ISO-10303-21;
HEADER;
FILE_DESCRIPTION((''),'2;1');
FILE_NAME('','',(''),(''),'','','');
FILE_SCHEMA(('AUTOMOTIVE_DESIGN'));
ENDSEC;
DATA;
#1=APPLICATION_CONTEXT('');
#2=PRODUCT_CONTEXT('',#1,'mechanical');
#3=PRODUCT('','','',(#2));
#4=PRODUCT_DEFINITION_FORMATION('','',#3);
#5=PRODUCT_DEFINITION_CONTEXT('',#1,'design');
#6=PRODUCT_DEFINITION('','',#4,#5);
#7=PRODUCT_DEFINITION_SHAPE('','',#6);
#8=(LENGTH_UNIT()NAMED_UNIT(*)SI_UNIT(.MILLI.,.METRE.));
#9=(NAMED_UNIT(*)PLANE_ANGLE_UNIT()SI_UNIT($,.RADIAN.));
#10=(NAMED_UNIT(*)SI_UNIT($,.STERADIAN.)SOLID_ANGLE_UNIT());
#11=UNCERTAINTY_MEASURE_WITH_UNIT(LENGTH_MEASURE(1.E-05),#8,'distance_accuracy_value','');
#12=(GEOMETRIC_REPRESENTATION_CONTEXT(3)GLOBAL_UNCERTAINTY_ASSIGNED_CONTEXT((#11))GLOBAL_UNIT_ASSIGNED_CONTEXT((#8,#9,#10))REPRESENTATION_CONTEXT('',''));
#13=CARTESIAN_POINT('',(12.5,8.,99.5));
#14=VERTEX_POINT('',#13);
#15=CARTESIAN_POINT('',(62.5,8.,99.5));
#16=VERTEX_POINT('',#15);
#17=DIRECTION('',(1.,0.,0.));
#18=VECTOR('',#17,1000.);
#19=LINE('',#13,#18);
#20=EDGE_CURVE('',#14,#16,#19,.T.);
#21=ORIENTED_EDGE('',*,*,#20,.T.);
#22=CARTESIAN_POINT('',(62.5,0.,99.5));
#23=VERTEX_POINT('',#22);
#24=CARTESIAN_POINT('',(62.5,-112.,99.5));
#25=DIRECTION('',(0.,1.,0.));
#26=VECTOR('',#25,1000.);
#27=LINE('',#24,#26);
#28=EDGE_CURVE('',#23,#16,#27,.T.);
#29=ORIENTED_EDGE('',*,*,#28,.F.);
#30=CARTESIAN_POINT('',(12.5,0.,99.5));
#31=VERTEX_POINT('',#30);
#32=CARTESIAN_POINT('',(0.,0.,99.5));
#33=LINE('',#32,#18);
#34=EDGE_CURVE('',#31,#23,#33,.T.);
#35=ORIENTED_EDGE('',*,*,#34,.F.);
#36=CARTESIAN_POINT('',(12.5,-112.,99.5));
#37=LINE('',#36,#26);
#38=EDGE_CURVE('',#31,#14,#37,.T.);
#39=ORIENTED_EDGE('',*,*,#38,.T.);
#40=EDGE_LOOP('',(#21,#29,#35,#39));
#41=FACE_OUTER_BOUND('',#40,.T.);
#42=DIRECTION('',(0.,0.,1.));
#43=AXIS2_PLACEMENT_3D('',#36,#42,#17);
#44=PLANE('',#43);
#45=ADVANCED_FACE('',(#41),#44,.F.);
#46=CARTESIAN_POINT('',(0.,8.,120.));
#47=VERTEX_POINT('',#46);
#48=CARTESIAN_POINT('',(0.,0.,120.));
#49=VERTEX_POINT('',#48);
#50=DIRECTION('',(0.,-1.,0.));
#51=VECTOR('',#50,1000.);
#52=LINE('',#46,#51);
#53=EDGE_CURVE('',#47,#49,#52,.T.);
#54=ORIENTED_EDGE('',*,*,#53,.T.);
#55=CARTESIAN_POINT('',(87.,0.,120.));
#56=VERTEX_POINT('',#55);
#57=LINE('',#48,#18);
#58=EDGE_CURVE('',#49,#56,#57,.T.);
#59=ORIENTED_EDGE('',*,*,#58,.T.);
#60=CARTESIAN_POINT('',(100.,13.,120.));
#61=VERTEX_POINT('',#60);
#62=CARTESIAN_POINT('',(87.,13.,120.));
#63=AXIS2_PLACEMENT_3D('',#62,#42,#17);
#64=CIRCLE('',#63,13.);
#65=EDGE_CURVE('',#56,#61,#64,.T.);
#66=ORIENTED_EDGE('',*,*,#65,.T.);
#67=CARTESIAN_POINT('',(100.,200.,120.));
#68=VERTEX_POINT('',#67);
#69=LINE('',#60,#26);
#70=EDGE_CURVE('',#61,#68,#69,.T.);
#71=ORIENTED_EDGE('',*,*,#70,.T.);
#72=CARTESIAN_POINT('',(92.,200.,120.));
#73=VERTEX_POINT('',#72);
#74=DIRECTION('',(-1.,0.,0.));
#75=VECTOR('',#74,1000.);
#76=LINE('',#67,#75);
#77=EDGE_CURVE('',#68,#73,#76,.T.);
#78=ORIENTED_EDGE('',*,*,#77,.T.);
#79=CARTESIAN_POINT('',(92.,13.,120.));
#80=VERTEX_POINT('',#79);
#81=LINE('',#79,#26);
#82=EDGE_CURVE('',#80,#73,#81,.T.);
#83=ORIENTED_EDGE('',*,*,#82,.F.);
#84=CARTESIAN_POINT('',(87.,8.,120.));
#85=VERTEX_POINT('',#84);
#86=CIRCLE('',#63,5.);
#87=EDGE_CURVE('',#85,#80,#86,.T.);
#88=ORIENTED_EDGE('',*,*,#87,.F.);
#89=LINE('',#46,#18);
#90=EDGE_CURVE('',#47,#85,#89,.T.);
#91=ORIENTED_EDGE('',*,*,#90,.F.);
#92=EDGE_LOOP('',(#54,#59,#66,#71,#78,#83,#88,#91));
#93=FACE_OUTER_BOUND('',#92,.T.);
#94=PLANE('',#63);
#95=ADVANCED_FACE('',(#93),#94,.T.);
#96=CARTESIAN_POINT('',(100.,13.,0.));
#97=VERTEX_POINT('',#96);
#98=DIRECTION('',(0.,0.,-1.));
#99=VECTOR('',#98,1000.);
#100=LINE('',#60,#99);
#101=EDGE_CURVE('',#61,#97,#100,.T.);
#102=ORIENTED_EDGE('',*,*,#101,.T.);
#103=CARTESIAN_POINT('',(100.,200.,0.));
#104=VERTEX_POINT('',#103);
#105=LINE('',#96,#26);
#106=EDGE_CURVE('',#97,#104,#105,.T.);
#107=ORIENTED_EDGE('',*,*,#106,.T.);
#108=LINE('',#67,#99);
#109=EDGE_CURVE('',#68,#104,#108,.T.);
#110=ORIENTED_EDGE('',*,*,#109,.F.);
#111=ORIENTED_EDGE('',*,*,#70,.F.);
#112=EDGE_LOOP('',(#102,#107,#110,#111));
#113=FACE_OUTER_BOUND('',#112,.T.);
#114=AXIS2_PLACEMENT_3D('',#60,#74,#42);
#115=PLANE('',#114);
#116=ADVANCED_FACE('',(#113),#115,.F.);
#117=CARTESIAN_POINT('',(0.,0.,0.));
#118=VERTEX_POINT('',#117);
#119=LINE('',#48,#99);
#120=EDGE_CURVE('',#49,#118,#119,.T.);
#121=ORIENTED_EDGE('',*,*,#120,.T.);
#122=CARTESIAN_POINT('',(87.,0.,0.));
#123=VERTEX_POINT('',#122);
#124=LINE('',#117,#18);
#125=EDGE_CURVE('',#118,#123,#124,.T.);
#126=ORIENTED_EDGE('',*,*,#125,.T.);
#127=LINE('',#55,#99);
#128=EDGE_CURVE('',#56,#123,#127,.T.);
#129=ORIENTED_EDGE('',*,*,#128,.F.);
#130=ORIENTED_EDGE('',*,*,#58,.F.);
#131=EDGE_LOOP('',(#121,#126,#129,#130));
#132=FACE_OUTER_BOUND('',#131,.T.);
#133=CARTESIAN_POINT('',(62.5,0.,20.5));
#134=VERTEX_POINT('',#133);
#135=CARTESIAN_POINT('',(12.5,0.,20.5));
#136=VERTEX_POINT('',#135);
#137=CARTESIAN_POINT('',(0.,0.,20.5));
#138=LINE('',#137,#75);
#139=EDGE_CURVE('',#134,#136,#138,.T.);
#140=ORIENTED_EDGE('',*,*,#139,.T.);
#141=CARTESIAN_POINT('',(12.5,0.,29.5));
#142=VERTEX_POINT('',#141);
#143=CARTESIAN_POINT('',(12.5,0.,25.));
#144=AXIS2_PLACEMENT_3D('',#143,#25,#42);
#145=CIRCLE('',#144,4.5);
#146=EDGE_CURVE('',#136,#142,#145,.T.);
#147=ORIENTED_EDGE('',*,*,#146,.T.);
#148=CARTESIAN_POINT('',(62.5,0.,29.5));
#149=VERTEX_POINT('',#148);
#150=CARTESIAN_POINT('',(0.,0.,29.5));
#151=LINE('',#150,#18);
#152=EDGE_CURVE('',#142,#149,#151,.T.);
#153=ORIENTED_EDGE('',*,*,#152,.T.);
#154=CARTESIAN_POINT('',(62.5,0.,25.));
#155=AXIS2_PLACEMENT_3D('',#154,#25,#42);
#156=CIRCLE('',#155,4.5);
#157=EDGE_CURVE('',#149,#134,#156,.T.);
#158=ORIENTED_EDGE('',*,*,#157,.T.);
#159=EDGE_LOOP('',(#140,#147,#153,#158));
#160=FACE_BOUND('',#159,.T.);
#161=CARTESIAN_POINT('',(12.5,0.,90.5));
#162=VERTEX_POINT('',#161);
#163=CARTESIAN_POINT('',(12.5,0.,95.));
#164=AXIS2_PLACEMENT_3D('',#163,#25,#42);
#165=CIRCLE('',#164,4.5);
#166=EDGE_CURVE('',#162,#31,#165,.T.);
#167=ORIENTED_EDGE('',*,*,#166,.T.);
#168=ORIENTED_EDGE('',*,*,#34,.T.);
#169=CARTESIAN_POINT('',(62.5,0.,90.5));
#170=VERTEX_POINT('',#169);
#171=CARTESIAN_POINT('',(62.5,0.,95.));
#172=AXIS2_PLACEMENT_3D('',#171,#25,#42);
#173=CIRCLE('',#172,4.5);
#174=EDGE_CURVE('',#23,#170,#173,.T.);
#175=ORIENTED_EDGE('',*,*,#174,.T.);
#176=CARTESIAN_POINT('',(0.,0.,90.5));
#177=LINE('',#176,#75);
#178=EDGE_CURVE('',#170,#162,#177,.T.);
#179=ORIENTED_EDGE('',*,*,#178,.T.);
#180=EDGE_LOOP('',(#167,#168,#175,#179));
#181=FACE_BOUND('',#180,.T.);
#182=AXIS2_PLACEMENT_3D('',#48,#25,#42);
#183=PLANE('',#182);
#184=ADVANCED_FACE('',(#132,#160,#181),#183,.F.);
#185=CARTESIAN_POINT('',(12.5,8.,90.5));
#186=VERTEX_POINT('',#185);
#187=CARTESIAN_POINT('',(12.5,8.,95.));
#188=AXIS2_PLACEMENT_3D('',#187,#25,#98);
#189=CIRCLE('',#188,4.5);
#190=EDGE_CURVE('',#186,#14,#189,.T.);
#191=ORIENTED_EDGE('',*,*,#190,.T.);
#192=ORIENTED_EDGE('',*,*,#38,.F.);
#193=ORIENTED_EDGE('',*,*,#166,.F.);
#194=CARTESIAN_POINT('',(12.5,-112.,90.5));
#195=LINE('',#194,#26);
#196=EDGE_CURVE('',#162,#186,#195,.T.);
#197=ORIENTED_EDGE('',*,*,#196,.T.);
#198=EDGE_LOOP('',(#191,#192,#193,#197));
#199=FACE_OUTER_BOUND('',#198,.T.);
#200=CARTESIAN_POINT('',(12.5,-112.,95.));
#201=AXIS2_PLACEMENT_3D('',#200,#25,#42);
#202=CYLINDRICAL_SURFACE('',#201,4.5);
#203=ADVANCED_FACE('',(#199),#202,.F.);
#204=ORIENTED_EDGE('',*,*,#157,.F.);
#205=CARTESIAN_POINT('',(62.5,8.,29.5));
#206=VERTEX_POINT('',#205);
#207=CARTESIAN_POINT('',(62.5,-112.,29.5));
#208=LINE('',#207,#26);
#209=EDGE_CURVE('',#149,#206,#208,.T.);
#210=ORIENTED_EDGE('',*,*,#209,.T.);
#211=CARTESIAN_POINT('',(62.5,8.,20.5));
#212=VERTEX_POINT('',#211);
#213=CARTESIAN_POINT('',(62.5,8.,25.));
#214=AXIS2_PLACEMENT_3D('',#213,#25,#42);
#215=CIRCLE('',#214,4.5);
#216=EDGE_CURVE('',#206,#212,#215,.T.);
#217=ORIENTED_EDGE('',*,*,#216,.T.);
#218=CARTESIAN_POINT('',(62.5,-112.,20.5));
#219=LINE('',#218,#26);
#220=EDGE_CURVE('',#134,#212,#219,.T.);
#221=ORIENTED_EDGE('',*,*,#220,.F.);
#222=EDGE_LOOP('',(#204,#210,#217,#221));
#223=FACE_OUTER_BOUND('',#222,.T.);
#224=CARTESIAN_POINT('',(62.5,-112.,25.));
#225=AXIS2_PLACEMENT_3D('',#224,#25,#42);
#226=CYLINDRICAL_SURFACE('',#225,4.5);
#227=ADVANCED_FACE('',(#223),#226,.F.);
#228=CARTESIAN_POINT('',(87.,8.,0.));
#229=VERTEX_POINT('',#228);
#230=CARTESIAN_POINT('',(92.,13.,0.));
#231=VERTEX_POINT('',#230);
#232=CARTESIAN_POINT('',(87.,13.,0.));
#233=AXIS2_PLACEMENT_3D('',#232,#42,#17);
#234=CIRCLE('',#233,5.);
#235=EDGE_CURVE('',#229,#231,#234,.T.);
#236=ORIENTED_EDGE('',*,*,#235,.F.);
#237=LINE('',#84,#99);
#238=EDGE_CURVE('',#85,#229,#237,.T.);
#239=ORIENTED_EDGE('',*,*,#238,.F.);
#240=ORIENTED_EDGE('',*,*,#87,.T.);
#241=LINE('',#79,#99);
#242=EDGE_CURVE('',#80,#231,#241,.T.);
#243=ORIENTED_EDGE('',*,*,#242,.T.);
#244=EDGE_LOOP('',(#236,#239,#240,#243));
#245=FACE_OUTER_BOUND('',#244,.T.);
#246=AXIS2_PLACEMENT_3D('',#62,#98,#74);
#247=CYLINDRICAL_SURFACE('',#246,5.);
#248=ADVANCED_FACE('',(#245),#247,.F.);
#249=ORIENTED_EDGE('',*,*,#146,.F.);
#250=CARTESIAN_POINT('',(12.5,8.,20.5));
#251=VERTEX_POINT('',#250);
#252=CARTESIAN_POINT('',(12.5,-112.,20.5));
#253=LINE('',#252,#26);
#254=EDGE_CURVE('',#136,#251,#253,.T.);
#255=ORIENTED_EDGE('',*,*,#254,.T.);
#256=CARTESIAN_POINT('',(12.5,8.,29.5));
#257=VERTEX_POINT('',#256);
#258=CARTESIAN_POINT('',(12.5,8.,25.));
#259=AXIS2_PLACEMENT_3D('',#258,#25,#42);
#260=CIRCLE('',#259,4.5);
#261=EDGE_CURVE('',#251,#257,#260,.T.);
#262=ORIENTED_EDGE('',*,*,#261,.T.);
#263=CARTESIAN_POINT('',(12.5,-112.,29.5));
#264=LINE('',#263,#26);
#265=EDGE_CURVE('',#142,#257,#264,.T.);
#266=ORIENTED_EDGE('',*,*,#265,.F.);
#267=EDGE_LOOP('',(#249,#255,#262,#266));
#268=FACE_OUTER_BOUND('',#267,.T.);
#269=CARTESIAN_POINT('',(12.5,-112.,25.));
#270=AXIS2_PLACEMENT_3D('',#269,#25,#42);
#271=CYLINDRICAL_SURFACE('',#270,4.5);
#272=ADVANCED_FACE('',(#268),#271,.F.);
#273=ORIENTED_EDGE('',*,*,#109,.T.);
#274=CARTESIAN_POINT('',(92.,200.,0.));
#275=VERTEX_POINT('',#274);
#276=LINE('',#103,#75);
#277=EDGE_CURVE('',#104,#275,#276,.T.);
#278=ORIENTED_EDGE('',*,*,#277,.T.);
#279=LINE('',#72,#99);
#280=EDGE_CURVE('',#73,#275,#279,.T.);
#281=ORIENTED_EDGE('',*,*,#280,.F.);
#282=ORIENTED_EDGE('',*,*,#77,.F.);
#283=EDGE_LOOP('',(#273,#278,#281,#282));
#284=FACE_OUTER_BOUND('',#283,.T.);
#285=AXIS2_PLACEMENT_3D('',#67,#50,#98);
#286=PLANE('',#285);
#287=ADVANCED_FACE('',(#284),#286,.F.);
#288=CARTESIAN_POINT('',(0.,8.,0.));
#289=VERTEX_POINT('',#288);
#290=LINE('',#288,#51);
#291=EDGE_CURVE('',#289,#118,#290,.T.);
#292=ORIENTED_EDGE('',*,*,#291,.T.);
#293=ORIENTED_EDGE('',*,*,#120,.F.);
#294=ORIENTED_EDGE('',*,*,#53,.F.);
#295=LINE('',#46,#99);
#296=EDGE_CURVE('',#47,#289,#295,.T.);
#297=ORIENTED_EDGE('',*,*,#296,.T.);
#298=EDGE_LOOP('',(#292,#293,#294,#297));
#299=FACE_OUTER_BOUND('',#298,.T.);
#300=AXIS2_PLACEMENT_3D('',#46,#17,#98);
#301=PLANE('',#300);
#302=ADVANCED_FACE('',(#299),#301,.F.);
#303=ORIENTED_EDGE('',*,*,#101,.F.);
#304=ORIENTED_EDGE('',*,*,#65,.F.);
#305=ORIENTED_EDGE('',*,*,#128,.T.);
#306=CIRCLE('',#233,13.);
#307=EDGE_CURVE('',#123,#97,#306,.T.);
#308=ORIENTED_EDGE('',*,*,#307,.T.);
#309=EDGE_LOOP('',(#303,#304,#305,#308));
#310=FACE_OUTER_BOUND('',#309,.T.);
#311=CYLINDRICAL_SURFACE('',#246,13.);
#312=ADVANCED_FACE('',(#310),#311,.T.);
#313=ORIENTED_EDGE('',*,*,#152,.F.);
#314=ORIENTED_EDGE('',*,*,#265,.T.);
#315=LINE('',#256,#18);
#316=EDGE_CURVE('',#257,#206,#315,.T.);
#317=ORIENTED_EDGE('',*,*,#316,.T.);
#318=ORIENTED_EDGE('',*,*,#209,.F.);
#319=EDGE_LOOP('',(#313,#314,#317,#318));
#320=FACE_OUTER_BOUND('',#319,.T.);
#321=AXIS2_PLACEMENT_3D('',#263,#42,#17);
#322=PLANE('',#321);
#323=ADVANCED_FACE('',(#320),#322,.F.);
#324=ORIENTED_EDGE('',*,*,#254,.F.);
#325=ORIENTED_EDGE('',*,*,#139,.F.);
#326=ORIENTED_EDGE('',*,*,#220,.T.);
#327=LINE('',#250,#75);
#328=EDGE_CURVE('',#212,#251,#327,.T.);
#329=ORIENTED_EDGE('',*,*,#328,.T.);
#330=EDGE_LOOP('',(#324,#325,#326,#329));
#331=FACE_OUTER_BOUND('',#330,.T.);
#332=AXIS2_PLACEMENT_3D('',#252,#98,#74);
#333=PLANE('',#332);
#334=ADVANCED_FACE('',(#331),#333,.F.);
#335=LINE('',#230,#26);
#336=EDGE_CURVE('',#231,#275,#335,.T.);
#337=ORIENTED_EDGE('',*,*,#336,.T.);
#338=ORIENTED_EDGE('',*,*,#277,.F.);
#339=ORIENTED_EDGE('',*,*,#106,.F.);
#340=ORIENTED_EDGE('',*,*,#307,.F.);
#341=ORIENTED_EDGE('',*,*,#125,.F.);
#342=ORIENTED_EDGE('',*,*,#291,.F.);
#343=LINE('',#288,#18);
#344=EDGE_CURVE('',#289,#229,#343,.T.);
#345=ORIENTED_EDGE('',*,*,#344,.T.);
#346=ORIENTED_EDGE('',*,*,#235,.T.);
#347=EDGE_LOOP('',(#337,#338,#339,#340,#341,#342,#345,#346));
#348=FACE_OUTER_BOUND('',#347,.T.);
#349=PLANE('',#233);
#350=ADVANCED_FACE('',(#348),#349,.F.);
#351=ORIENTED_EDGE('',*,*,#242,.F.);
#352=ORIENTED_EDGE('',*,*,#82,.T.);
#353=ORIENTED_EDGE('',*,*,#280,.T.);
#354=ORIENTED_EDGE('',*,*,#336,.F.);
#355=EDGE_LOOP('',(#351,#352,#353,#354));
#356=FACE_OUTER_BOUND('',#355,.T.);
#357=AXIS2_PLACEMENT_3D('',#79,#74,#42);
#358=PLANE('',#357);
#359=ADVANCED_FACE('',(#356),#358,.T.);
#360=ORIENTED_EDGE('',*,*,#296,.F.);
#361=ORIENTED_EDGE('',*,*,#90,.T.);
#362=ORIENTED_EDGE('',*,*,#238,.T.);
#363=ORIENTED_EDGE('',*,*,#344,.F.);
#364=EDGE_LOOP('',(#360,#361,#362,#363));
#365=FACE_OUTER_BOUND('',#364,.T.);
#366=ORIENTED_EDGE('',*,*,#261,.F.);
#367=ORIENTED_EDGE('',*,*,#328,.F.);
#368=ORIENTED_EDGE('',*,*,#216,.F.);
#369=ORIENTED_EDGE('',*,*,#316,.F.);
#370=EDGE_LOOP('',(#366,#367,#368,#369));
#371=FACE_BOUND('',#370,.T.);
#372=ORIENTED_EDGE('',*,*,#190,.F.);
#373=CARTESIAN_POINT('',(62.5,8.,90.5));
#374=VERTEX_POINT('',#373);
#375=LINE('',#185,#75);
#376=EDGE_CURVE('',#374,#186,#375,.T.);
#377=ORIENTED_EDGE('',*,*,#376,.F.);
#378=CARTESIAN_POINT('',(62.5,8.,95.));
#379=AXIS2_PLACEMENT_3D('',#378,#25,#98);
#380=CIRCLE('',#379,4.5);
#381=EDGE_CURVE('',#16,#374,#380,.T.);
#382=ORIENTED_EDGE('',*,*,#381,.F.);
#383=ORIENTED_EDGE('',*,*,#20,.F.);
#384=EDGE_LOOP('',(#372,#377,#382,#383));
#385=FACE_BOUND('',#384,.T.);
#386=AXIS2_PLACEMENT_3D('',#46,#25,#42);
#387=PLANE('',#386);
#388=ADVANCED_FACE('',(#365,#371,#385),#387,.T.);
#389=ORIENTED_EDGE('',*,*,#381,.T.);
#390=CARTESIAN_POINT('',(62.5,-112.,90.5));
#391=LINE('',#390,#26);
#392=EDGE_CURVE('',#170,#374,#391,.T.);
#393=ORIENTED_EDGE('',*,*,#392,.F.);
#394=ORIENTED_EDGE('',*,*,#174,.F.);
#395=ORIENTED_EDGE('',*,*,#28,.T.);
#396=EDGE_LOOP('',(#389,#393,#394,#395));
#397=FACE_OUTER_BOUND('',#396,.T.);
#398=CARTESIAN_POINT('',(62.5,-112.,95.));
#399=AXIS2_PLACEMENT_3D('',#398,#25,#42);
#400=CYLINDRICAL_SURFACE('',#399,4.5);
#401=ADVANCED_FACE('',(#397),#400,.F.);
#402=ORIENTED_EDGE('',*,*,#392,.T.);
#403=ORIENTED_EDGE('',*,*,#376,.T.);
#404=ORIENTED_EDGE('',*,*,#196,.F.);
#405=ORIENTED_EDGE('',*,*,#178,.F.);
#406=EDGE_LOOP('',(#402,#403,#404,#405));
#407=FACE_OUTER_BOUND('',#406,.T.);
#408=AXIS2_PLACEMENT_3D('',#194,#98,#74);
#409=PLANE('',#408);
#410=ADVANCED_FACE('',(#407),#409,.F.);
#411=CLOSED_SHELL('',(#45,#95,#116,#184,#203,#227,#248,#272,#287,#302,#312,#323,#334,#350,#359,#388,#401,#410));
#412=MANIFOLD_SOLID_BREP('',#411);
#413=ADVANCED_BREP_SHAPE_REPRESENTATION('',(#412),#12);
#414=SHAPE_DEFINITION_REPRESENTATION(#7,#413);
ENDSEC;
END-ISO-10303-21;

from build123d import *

# Parameters (mm, degrees)
BOSS_EXTRUDE1_DEPTH = 120
CUT_EXTRUDE1_DEPTH  = 120


with BuildPart() as part:
    # Sketch1 → Boss-Extrude1 (new body)
    with BuildSketch(Plane.XY):
        with BuildLine():
            Line((0, 0), (87, 0))
            ThreePointArc((87, 0), (96.192388155, 3.807611845), (100, 13))
            Line((100, 13), (100, 200))
            Line((100, 200), (92, 200))
            Line((92, 200), (92, 13))
            ThreePointArc((92, 13), (90.535533906, 9.464466094), (87, 8))
            Line((87, 8), (0, 8))
            Line((0, 8), (0, 0))
        make_face()
    extrude(amount=BOSS_EXTRUDE1_DEPTH)

    # Sketch2 → Cut-Extrude1 (cut)
    with BuildSketch(Plane(origin=(0, 8, 0), x_dir=(1, 0, 0), z_dir=(0, 1, 0))):
        with BuildLine():
            Line((12.5, -20.5), (62.5, -20.5))
            ThreePointArc((62.5, -20.5), (67, -25), (62.5, -29.5))
            Line((62.5, -29.5), (12.5, -29.5))
            ThreePointArc((12.5, -29.5), (8, -25), (12.5, -20.5))
        make_face()
        with BuildLine():
            Line((12.5, -99.5), (62.5, -99.5))
            ThreePointArc((62.5, -99.5), (67, -95), (62.5, -90.5))
            Line((62.5, -90.5), (12.5, -90.5))
            ThreePointArc((12.5, -90.5), (8, -95), (12.5, -99.5))
        make_face()
    extrude(amount=-CUT_EXTRUDE1_DEPTH, mode=Mode.SUBTRACT)


solid = part.part
